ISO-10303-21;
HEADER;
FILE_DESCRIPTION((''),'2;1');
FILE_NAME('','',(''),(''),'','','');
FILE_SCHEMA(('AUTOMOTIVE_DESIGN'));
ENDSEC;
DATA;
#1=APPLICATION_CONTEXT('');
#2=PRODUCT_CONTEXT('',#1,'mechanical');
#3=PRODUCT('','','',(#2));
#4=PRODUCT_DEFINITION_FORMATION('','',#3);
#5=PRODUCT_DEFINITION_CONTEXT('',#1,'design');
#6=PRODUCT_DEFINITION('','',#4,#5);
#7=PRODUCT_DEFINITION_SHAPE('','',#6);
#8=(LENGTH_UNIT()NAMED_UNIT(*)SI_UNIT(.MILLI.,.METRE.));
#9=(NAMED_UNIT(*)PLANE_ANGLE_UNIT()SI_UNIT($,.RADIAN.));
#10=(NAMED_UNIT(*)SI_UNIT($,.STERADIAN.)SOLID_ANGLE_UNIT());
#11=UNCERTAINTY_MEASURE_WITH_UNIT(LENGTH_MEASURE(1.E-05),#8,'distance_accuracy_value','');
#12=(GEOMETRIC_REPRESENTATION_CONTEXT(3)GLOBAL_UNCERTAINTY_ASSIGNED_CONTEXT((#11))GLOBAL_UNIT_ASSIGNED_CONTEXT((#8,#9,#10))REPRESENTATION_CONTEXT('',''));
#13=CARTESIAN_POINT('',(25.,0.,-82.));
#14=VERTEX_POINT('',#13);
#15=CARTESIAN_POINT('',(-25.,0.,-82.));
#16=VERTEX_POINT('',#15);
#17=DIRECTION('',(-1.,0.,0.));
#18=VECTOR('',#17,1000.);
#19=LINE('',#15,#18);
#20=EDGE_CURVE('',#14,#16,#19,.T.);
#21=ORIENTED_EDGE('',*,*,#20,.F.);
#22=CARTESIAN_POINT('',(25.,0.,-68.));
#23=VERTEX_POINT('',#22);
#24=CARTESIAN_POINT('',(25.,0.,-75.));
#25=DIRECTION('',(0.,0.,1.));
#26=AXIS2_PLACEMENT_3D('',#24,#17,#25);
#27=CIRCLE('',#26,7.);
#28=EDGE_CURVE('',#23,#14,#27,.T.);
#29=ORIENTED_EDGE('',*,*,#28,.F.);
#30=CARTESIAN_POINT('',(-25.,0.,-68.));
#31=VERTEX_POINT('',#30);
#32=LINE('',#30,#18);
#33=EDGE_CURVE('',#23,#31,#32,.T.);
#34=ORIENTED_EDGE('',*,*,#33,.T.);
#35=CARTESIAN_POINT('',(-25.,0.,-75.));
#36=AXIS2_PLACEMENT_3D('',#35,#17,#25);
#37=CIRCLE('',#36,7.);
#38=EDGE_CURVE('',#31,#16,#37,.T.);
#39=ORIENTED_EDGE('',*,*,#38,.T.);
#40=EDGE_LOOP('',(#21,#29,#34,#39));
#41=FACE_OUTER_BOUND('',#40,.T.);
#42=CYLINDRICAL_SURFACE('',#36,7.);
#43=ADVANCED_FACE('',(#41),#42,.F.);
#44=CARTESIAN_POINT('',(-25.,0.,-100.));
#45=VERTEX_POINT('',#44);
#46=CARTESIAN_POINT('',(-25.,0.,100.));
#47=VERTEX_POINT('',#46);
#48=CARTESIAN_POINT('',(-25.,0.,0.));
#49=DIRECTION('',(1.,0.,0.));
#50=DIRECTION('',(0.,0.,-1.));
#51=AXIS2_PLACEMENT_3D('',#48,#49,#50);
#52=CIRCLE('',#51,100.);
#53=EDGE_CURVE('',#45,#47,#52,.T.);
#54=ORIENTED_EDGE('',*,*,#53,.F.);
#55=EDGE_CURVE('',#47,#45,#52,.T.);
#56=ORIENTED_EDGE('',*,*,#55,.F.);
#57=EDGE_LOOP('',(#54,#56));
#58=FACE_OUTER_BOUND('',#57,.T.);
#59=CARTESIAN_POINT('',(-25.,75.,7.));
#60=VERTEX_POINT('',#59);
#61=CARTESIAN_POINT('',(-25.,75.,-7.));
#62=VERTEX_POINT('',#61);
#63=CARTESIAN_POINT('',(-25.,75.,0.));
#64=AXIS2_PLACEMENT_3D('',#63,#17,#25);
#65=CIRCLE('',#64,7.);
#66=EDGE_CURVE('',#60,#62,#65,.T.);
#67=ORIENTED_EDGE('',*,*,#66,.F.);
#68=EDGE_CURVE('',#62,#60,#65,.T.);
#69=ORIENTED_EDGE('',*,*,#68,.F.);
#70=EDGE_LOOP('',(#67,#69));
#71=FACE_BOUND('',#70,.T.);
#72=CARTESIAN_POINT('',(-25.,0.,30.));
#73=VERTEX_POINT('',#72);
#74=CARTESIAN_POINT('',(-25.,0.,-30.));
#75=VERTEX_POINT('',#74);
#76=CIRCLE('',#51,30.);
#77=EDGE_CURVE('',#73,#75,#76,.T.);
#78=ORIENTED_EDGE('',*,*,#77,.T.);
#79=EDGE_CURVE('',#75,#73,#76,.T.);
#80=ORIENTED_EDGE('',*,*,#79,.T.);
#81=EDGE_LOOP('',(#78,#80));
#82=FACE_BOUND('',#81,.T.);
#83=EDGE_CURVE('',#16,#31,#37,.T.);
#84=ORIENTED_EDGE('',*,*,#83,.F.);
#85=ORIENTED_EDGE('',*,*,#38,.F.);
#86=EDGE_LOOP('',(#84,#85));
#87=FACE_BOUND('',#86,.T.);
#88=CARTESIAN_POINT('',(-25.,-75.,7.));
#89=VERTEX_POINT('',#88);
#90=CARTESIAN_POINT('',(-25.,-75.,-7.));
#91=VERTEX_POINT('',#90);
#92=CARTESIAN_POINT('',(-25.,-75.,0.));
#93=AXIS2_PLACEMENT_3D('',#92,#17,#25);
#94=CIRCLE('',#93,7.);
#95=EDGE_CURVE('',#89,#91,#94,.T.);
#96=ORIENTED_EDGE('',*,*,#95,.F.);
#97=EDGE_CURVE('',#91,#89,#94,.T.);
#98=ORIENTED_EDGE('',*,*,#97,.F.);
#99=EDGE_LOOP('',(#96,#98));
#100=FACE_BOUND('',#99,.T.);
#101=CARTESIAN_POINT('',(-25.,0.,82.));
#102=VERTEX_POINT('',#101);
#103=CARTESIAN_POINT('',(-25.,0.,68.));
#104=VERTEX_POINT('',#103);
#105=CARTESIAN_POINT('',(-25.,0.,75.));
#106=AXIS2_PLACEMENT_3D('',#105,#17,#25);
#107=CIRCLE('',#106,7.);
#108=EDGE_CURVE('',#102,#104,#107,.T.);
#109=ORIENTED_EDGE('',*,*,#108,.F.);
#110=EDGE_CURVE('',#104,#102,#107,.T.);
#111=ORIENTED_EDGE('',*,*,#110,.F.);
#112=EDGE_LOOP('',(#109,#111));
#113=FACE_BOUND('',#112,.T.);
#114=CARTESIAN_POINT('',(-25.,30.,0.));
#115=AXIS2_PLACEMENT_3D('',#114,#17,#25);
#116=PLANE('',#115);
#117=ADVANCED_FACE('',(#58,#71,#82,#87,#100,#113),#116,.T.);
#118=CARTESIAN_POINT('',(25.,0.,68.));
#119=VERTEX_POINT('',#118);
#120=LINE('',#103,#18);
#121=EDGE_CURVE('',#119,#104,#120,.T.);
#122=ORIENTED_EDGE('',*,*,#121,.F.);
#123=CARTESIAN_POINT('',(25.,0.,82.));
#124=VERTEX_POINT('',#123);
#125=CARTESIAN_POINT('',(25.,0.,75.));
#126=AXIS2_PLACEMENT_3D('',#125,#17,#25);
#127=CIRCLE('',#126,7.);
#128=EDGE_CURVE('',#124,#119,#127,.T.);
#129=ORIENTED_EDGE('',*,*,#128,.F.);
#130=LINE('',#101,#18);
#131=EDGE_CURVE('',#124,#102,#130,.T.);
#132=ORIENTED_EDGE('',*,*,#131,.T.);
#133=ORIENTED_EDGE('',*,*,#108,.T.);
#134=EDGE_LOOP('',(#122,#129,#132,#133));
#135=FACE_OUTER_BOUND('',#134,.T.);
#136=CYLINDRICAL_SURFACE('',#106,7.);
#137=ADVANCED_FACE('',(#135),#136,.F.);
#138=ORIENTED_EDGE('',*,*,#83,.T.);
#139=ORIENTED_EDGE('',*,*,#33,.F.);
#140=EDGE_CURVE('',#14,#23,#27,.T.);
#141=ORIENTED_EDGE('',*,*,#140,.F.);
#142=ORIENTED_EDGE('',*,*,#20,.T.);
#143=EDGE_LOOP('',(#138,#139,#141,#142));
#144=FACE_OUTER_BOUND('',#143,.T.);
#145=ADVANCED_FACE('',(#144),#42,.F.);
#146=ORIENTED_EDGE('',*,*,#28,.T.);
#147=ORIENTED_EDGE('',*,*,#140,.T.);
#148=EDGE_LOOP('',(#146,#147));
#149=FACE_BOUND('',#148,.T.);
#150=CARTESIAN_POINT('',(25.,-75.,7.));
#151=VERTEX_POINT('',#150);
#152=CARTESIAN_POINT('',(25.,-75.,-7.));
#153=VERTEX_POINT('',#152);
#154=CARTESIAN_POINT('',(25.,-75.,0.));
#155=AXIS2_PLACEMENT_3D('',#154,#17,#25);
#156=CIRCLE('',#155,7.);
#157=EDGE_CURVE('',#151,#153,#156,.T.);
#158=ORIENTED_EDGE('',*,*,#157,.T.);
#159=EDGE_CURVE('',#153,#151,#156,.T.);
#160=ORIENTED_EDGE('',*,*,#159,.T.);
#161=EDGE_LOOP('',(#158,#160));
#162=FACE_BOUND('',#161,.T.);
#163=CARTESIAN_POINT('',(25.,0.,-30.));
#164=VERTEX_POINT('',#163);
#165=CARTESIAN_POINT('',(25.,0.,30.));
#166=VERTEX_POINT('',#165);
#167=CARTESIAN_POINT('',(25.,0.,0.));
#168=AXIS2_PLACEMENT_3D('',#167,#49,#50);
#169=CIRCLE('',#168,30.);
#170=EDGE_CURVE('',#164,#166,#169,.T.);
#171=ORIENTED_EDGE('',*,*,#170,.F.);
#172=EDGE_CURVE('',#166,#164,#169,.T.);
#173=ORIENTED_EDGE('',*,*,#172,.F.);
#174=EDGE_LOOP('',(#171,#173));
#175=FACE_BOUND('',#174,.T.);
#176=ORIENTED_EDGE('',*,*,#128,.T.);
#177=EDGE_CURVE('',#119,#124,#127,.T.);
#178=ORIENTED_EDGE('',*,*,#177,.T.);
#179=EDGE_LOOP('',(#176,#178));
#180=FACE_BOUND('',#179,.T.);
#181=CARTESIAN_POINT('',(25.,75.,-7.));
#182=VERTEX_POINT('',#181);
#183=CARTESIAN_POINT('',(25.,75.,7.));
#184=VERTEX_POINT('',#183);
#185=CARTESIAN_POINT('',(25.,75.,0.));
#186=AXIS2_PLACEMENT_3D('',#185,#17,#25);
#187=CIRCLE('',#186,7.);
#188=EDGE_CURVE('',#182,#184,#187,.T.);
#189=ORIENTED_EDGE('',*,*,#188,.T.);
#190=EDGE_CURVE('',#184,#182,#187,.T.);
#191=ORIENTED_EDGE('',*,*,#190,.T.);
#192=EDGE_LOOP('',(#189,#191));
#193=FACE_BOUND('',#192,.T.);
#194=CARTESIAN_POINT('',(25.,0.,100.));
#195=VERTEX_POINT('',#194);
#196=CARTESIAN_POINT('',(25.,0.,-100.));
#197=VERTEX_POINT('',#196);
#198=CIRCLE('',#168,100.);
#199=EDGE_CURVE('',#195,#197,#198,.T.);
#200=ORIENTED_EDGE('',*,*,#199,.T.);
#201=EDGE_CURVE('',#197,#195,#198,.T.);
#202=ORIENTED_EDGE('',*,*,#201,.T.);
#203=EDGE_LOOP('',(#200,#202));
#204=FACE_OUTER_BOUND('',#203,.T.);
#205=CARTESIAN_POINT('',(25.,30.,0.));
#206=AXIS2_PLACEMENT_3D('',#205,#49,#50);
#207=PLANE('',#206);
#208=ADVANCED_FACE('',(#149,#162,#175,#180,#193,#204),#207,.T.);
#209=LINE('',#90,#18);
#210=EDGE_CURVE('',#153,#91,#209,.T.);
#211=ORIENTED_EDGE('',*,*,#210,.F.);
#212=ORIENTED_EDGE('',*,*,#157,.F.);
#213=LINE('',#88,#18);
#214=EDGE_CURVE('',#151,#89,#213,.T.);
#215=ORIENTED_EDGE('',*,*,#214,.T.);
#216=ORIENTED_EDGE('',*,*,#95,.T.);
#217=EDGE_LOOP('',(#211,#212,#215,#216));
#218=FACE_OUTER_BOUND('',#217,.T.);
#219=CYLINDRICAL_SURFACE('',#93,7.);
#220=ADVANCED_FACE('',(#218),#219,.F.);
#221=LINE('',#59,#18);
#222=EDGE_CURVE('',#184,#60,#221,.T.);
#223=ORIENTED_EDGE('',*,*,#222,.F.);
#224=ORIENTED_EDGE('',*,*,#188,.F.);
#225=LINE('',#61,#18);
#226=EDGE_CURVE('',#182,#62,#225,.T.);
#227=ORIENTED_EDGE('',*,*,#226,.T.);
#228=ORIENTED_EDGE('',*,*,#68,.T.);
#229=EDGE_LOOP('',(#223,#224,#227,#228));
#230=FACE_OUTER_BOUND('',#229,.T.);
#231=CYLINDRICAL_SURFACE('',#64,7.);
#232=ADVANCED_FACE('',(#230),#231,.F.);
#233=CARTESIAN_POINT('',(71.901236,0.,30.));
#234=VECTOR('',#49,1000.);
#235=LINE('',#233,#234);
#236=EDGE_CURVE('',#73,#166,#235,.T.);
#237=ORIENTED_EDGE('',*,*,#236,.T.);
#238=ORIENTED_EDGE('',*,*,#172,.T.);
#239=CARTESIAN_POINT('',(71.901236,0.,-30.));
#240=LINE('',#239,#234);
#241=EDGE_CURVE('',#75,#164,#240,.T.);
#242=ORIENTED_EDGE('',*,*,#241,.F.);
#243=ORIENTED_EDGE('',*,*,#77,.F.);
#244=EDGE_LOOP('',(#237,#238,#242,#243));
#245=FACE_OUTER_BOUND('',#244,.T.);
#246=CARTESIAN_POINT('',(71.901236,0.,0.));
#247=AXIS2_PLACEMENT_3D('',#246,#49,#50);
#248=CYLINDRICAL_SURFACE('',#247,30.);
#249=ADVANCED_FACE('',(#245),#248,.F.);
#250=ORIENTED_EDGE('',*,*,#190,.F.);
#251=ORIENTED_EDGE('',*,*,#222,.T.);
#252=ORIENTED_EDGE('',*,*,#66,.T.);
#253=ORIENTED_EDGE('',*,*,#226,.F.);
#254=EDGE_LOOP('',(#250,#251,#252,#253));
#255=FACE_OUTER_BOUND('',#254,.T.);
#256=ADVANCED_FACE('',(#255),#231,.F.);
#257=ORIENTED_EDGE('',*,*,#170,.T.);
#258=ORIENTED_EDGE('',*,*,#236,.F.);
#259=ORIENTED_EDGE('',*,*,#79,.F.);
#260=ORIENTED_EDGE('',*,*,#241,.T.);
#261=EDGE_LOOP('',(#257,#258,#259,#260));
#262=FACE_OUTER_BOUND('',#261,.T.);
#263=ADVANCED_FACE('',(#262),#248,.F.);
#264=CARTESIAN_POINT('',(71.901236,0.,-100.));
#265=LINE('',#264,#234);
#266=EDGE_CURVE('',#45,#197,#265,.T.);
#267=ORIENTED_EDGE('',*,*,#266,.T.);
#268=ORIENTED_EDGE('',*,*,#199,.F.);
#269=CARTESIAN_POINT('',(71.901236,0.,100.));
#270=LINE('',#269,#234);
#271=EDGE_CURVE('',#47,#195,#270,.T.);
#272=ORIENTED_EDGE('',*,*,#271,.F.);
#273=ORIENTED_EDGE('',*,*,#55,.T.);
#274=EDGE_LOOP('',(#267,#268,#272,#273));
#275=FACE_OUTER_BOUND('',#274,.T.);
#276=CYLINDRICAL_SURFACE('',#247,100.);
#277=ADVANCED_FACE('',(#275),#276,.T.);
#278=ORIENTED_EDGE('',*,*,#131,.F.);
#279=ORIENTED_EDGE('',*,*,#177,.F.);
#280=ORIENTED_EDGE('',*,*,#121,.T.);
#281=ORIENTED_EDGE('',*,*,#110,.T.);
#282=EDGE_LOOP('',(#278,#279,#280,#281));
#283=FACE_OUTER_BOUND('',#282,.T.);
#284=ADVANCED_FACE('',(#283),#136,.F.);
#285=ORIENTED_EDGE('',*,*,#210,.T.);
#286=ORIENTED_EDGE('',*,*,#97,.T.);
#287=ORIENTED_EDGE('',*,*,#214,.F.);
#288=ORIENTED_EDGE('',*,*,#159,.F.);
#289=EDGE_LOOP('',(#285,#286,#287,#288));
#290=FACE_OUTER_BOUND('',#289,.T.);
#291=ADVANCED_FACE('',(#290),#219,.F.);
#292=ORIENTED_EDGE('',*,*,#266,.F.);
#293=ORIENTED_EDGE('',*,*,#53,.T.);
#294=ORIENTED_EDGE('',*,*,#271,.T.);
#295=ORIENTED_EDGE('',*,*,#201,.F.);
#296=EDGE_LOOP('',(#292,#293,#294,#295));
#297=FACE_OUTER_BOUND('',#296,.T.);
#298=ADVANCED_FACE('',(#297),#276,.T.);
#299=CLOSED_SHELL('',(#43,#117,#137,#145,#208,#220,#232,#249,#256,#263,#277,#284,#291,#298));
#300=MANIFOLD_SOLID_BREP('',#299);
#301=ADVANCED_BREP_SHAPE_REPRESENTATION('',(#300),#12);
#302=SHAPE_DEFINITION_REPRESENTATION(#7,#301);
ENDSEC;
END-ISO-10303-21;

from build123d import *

# Parameters (mm, degrees)
SKETCH1_W          = 50
SKETCH1_H          = 70
M16_TAPPED_HOLE1_D = 14
CIRPATTERN1_COUNT  = 4


with BuildPart() as part:
    # Sketch1 → Revolve1 (revolve)
    with BuildSketch(Plane.XY, mode=Mode.PRIVATE) as revolve1_sk:
        with Locations((0, 65)):
            Rectangle(SKETCH1_W, SKETCH1_H)
    revolve(revolve1_sk.sketch.rotate(Axis((71.901236476, 0, 0), (-1, 0, 0)), 90), axis=Axis((71.901236476, 0, 0), (-1, 0, 0)))

    # M16 Tapped Hole1 (through all)
    with Locations(Plane(origin=(-25, 0, -75), x_dir=(0, 0, -1), z_dir=(-1, 0, 0))):
        with Locations((0, 0)):
            m16_tapped_hole1 = Hole(M16_TAPPED_HOLE1_D / 2)

    # CirPattern1: M16 Tapped Hole1 ×4 about axis
    cirpattern1_axis = Axis((0, 0, 0), (1, 0, 0))
    for i in range(1, CIRPATTERN1_COUNT):
        add(m16_tapped_hole1.rotate(cirpattern1_axis, i * 360 / CIRPATTERN1_COUNT), mode=Mode.SUBTRACT)


solid = part.part
